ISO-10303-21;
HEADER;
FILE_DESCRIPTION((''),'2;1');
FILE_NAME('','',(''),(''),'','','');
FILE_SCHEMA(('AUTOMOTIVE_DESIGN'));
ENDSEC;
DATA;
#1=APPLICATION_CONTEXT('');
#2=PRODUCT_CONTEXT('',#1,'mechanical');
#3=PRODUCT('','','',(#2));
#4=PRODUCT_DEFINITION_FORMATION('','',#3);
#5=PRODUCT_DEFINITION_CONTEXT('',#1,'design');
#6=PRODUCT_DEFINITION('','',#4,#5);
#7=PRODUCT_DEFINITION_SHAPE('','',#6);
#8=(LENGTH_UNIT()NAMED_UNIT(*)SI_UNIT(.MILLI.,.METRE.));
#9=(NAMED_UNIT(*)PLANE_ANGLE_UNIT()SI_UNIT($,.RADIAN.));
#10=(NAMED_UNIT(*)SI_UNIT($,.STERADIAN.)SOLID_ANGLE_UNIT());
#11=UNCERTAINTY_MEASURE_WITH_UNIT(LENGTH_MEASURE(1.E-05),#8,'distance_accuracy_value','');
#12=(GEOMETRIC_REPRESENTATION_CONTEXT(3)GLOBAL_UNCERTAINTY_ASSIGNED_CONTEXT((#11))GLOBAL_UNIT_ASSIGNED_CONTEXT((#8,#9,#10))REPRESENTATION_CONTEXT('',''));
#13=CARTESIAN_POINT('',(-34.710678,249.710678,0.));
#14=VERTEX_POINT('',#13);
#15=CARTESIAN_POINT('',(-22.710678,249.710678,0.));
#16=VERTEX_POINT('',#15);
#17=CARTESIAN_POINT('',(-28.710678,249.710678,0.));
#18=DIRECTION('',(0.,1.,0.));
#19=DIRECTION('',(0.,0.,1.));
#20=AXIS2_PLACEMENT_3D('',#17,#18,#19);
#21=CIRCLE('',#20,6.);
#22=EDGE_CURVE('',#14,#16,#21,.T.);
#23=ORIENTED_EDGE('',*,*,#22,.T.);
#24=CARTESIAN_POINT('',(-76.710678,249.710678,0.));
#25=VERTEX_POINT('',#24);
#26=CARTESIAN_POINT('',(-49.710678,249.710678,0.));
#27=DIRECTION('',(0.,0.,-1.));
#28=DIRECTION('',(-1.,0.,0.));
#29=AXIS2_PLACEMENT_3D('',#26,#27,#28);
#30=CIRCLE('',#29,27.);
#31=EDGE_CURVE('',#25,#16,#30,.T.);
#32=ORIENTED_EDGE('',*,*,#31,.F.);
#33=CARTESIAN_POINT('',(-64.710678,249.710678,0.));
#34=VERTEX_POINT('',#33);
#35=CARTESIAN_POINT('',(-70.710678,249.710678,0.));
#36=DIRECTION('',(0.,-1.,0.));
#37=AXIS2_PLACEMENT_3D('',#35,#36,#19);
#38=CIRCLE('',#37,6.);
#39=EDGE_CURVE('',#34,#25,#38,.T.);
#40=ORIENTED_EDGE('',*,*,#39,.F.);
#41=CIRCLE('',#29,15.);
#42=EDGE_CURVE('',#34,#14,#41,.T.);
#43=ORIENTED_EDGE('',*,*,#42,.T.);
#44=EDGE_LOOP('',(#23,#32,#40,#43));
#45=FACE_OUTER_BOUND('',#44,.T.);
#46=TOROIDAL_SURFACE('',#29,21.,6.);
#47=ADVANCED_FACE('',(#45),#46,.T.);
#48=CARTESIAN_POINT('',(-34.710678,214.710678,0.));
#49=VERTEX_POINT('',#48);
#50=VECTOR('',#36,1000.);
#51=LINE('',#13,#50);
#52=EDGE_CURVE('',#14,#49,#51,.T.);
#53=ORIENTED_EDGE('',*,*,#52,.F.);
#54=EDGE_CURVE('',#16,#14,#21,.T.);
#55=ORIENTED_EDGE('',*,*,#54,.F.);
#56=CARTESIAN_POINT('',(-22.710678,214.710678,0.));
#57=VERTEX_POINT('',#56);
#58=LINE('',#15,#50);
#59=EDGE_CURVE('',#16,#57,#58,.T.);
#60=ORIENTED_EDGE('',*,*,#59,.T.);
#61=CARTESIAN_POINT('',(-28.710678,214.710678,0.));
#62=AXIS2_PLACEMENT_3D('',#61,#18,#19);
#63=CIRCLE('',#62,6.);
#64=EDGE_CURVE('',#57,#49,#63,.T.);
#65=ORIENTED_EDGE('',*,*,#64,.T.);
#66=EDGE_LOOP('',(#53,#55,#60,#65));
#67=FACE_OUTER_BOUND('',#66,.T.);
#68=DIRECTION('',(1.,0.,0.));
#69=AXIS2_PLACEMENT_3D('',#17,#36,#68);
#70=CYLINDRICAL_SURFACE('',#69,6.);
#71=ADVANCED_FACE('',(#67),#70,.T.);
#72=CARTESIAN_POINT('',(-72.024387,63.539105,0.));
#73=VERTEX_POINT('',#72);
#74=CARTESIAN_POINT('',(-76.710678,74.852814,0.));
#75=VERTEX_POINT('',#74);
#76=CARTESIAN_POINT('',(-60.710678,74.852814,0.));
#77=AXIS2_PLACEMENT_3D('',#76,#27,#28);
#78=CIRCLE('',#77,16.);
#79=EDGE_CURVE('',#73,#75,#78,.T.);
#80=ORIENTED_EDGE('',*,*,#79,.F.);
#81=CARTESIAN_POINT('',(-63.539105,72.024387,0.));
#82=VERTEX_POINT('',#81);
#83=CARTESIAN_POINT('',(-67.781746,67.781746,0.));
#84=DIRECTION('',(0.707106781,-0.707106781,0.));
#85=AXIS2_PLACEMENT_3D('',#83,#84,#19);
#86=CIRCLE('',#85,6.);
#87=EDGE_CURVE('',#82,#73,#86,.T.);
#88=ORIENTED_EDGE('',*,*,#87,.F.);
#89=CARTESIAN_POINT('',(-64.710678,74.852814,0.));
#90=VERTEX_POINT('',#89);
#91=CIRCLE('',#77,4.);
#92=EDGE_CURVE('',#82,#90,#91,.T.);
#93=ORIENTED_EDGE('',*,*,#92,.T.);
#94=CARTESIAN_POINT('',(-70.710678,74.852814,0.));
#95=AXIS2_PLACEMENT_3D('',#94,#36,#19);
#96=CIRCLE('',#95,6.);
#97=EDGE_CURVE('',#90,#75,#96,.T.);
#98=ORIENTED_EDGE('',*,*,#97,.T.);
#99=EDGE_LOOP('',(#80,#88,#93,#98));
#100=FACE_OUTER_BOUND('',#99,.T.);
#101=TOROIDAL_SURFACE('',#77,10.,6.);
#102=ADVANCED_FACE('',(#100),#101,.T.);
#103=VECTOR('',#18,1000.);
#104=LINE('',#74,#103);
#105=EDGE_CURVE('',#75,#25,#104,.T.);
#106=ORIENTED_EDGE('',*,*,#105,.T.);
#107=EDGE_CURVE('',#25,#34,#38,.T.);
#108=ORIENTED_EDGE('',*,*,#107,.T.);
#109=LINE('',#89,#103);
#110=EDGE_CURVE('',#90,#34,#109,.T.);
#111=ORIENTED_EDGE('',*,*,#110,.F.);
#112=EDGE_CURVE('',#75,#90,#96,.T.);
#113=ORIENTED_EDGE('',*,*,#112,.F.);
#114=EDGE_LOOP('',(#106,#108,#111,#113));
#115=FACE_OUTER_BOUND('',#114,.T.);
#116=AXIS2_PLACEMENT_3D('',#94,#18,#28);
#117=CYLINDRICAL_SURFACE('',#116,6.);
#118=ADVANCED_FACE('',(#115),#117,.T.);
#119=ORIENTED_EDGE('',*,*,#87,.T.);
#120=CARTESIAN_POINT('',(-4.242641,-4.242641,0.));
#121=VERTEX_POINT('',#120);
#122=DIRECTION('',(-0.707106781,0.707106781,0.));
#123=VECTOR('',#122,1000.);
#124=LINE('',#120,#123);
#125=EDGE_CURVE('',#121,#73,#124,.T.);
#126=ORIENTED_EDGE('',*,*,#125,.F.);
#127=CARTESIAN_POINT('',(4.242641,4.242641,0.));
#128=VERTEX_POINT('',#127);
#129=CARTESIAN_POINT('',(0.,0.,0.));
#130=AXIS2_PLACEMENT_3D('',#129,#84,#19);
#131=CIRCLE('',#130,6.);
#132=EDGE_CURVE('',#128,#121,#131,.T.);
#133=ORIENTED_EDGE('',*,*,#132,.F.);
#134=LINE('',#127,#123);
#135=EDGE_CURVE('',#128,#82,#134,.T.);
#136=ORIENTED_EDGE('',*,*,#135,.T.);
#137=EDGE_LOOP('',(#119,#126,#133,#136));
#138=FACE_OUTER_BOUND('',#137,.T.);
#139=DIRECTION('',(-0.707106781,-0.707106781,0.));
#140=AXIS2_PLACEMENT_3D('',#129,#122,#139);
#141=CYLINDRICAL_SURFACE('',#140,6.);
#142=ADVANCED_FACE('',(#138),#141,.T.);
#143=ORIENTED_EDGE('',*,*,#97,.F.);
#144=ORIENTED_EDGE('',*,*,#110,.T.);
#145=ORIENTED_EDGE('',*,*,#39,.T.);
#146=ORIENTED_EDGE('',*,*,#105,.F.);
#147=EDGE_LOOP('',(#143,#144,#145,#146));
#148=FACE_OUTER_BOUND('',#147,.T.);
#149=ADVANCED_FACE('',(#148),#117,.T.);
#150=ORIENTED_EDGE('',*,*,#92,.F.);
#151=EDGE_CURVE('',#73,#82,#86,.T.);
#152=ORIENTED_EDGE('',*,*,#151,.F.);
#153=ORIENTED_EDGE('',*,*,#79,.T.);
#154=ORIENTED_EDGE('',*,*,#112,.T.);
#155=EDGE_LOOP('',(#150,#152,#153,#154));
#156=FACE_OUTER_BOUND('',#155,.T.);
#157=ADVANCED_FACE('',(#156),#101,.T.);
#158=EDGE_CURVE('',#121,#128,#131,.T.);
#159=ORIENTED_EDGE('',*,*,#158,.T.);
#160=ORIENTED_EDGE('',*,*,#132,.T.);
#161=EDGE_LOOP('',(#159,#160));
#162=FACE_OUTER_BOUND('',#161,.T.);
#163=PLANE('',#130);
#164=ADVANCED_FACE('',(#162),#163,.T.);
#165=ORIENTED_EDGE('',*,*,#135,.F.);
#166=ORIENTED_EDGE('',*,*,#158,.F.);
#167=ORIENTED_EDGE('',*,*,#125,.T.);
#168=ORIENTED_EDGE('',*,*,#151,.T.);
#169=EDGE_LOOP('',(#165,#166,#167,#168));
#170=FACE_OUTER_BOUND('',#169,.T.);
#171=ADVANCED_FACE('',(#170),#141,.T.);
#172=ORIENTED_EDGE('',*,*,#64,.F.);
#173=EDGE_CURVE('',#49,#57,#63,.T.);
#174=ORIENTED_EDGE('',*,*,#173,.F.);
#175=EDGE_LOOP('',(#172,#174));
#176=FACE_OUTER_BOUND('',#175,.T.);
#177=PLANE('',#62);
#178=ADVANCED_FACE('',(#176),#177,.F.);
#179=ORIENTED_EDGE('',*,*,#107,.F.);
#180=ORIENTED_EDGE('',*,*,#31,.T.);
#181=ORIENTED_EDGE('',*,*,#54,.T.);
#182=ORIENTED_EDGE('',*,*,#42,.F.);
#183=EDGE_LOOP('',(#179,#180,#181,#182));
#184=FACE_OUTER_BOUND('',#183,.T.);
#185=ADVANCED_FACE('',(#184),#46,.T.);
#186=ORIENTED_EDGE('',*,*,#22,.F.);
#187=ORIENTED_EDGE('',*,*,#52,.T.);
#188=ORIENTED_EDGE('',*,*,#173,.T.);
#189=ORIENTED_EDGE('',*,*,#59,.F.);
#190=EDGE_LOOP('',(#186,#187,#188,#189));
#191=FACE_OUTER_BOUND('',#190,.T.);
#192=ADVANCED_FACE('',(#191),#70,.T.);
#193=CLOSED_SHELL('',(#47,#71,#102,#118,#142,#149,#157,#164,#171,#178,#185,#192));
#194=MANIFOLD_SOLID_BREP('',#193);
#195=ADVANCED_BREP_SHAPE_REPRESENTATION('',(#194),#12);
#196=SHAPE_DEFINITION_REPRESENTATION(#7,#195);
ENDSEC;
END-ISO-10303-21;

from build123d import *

# Parameters (mm, degrees)
SWEEP_1_PROFILE_R = 6


with BuildPart() as part:
    # 扫描1: sweep along a path in 草图1
    with BuildLine(Plane.XY) as sweep_1_path:
        Line((0, 0), (-67.781745931, 67.781745931))
        ThreePointArc((-67.781745931, 67.781745931), (-69.949473444, 71.025979419), (-70.710678119, 74.852813742))
        Line((-70.710678119, 74.852813742), (-70.710678119, 249.710678119))
        ThreePointArc((-70.710678119, 249.710678119), (-49.710678119, 270.710678119), (-28.710678119, 249.710678119))
        Line((-28.710678119, 249.710678119), (-28.710678119, 214.710678119))
    # 扫描1 profile (on start of the path) → 扫描1 (sweep)
    with BuildSketch(Plane(origin=(0, 0, 0), x_dir=(-0.7071067811865462, -0.7071067811865488, 0), z_dir=(-0.7071067811865488, 0.7071067811865462, 0))):
        Circle(SWEEP_1_PROFILE_R)
    sweep(path=sweep_1_path.line)


solid = part.part
